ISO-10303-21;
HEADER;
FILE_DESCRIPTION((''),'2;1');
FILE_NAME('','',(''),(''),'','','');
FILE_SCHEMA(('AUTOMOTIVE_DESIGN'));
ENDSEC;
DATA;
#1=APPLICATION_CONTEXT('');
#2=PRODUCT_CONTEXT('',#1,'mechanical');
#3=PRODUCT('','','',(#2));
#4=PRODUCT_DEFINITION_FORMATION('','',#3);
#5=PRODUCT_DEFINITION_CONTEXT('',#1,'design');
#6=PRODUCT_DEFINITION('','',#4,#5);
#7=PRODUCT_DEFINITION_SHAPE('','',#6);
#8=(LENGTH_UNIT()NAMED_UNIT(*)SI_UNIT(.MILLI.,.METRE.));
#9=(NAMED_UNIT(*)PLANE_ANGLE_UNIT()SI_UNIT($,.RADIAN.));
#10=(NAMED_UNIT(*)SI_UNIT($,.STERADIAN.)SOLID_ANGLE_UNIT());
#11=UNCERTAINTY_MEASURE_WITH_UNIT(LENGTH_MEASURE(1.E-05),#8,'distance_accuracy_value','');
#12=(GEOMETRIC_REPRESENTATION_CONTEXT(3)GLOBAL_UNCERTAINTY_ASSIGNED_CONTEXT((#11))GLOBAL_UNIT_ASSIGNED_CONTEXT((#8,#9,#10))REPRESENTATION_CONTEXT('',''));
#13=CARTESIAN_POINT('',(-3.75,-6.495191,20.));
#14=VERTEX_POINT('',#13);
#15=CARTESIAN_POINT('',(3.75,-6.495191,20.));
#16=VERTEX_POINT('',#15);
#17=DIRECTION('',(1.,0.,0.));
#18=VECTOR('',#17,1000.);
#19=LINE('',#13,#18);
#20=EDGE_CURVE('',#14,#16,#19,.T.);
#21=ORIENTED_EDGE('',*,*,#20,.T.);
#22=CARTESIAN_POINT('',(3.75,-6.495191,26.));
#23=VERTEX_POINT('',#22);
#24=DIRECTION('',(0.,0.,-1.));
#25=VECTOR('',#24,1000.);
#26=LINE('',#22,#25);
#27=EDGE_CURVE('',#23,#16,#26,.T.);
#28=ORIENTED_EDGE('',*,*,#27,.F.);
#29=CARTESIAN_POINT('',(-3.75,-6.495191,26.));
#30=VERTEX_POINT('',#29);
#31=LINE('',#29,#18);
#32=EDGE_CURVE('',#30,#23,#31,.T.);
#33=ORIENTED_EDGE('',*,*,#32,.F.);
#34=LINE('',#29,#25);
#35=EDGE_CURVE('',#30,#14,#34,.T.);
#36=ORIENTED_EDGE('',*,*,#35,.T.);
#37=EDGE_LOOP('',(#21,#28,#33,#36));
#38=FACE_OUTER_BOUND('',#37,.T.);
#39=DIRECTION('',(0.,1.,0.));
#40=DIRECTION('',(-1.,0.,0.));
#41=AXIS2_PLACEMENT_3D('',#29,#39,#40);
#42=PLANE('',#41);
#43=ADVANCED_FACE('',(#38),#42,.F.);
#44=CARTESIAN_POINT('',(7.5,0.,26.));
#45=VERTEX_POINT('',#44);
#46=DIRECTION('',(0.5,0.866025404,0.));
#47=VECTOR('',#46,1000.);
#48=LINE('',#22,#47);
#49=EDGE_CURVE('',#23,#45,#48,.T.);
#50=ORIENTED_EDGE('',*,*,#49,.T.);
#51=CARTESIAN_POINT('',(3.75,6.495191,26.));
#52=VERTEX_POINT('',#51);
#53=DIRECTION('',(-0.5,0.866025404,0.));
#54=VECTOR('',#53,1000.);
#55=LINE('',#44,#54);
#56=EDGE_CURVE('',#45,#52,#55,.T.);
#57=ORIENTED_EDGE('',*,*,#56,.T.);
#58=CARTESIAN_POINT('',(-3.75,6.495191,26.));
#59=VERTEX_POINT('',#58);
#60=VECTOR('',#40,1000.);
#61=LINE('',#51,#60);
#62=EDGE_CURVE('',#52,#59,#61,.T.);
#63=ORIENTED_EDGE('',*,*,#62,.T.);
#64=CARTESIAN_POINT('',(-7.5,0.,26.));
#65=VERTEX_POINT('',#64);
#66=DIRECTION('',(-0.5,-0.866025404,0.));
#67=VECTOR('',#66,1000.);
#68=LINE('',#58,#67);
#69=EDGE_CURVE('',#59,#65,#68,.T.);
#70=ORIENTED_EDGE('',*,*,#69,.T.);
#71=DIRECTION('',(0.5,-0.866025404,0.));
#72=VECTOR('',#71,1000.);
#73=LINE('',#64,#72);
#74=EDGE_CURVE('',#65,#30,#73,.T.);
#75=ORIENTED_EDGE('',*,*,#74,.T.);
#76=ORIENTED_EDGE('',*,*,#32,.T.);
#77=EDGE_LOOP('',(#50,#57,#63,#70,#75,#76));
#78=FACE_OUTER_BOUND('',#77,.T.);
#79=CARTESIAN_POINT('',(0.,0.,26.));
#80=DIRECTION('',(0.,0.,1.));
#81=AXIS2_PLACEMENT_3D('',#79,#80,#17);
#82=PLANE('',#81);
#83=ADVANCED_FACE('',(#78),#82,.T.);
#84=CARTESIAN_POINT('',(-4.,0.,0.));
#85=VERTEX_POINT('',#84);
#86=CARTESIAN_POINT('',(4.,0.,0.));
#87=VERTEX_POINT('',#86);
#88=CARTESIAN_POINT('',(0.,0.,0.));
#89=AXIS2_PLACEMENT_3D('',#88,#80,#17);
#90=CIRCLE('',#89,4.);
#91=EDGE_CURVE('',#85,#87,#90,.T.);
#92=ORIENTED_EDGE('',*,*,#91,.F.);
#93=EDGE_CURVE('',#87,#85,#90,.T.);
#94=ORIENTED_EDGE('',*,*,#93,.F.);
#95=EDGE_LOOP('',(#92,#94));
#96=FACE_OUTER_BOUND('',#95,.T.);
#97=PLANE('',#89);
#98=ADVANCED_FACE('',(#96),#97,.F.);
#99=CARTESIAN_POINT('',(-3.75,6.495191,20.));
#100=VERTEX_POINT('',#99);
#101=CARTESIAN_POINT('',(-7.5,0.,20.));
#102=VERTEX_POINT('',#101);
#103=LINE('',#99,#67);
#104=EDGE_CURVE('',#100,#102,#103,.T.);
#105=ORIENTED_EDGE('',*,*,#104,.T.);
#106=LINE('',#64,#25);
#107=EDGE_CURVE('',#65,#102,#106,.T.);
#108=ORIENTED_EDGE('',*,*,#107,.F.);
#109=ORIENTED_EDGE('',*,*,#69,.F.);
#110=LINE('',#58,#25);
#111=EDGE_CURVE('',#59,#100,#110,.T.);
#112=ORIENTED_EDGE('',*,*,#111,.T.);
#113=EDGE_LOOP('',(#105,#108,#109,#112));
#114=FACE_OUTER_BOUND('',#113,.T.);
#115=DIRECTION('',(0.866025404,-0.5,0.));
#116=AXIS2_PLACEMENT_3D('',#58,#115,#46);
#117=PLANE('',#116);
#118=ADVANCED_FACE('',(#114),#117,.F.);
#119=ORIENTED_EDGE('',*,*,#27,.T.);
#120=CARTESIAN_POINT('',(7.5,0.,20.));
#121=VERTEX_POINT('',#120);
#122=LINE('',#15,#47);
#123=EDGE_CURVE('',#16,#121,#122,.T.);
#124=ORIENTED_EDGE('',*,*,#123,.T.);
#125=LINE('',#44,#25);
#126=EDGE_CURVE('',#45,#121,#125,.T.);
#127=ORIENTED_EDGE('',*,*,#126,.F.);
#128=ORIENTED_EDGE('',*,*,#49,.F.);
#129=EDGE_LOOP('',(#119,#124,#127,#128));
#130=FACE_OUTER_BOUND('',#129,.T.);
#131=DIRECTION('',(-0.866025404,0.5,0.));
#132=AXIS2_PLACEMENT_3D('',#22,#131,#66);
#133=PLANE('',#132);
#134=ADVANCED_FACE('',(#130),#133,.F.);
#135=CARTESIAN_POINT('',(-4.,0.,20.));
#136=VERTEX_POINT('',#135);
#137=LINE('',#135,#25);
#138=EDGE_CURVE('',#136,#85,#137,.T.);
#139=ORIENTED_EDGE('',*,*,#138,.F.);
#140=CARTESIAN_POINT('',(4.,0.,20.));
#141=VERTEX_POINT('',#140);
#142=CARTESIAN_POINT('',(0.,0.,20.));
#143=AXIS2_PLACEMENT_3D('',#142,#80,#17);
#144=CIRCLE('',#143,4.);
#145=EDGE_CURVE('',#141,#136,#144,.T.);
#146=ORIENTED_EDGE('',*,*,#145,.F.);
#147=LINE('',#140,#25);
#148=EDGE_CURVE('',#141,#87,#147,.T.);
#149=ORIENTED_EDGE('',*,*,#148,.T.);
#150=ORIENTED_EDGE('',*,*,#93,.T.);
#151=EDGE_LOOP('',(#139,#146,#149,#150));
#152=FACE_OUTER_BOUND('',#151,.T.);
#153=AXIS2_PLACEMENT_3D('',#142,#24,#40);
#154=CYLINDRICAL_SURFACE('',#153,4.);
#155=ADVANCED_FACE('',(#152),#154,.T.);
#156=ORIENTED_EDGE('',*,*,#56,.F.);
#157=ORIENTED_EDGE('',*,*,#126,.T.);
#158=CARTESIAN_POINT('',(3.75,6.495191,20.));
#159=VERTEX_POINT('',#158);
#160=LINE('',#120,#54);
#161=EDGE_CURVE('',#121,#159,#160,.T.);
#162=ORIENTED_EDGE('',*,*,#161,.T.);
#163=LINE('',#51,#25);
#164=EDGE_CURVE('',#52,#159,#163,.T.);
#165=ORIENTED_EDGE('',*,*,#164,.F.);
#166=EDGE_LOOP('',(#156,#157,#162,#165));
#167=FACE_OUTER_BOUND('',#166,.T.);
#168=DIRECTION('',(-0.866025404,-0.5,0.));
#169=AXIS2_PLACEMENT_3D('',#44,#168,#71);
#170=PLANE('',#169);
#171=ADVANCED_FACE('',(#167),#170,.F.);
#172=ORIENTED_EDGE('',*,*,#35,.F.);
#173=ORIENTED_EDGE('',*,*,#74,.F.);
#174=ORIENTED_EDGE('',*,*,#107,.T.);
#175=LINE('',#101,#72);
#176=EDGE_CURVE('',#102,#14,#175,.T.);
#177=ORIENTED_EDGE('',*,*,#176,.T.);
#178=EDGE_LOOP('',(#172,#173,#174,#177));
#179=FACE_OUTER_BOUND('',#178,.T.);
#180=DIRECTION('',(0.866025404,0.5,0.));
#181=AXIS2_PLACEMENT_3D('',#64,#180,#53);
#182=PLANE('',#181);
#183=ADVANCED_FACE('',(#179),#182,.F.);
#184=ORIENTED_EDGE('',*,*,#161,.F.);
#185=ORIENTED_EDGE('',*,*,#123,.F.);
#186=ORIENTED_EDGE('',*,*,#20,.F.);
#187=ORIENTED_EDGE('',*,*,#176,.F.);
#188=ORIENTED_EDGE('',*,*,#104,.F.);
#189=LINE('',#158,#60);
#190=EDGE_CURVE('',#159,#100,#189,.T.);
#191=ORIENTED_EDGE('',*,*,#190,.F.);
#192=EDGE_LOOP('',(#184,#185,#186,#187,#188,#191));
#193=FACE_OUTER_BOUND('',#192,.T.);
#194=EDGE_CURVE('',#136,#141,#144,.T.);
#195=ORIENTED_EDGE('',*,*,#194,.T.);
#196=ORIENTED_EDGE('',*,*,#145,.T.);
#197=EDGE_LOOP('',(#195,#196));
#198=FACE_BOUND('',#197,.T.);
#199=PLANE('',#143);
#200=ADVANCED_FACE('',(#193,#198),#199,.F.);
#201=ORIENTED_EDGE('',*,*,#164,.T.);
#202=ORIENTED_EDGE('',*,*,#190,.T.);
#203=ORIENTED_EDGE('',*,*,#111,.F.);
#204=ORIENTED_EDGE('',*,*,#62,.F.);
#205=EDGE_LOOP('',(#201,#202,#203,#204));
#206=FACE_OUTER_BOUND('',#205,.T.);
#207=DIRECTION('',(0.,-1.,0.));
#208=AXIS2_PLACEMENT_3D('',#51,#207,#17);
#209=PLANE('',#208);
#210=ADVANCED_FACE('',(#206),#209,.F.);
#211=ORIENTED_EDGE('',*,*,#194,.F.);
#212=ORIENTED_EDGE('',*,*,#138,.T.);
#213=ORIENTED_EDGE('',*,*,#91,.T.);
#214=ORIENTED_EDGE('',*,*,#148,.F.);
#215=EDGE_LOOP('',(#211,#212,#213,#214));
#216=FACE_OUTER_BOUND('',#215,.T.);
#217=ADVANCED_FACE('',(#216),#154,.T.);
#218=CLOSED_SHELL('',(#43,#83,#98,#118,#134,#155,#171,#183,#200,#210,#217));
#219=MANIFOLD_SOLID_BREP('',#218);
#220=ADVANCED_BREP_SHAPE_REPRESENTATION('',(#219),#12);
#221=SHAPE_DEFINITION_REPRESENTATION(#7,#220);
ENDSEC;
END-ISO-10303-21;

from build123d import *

# Parameters (mm, degrees)
SKETCH1_R           = 4
BOSS_EXTRUDE1_DEPTH = 20
BOSS_EXTRUDE2_DEPTH = 6


with BuildPart() as part:
    # Sketch1 → Boss-Extrude1 (new body)
    with BuildSketch(Plane.XY):
        Circle(SKETCH1_R)
    extrude(amount=BOSS_EXTRUDE1_DEPTH)

    # Sketch2 → Boss-Extrude2 (add)
    with BuildSketch(Plane.XY.offset(20)):
        Polygon((-3.75, 6.495190528), (-7.5, 0), (-3.75, -6.495190528), (3.75, -6.495190528), (7.5, 0), (3.75, 6.495190528), align=None)
    extrude(amount=BOSS_EXTRUDE2_DEPTH)


solid = part.part
